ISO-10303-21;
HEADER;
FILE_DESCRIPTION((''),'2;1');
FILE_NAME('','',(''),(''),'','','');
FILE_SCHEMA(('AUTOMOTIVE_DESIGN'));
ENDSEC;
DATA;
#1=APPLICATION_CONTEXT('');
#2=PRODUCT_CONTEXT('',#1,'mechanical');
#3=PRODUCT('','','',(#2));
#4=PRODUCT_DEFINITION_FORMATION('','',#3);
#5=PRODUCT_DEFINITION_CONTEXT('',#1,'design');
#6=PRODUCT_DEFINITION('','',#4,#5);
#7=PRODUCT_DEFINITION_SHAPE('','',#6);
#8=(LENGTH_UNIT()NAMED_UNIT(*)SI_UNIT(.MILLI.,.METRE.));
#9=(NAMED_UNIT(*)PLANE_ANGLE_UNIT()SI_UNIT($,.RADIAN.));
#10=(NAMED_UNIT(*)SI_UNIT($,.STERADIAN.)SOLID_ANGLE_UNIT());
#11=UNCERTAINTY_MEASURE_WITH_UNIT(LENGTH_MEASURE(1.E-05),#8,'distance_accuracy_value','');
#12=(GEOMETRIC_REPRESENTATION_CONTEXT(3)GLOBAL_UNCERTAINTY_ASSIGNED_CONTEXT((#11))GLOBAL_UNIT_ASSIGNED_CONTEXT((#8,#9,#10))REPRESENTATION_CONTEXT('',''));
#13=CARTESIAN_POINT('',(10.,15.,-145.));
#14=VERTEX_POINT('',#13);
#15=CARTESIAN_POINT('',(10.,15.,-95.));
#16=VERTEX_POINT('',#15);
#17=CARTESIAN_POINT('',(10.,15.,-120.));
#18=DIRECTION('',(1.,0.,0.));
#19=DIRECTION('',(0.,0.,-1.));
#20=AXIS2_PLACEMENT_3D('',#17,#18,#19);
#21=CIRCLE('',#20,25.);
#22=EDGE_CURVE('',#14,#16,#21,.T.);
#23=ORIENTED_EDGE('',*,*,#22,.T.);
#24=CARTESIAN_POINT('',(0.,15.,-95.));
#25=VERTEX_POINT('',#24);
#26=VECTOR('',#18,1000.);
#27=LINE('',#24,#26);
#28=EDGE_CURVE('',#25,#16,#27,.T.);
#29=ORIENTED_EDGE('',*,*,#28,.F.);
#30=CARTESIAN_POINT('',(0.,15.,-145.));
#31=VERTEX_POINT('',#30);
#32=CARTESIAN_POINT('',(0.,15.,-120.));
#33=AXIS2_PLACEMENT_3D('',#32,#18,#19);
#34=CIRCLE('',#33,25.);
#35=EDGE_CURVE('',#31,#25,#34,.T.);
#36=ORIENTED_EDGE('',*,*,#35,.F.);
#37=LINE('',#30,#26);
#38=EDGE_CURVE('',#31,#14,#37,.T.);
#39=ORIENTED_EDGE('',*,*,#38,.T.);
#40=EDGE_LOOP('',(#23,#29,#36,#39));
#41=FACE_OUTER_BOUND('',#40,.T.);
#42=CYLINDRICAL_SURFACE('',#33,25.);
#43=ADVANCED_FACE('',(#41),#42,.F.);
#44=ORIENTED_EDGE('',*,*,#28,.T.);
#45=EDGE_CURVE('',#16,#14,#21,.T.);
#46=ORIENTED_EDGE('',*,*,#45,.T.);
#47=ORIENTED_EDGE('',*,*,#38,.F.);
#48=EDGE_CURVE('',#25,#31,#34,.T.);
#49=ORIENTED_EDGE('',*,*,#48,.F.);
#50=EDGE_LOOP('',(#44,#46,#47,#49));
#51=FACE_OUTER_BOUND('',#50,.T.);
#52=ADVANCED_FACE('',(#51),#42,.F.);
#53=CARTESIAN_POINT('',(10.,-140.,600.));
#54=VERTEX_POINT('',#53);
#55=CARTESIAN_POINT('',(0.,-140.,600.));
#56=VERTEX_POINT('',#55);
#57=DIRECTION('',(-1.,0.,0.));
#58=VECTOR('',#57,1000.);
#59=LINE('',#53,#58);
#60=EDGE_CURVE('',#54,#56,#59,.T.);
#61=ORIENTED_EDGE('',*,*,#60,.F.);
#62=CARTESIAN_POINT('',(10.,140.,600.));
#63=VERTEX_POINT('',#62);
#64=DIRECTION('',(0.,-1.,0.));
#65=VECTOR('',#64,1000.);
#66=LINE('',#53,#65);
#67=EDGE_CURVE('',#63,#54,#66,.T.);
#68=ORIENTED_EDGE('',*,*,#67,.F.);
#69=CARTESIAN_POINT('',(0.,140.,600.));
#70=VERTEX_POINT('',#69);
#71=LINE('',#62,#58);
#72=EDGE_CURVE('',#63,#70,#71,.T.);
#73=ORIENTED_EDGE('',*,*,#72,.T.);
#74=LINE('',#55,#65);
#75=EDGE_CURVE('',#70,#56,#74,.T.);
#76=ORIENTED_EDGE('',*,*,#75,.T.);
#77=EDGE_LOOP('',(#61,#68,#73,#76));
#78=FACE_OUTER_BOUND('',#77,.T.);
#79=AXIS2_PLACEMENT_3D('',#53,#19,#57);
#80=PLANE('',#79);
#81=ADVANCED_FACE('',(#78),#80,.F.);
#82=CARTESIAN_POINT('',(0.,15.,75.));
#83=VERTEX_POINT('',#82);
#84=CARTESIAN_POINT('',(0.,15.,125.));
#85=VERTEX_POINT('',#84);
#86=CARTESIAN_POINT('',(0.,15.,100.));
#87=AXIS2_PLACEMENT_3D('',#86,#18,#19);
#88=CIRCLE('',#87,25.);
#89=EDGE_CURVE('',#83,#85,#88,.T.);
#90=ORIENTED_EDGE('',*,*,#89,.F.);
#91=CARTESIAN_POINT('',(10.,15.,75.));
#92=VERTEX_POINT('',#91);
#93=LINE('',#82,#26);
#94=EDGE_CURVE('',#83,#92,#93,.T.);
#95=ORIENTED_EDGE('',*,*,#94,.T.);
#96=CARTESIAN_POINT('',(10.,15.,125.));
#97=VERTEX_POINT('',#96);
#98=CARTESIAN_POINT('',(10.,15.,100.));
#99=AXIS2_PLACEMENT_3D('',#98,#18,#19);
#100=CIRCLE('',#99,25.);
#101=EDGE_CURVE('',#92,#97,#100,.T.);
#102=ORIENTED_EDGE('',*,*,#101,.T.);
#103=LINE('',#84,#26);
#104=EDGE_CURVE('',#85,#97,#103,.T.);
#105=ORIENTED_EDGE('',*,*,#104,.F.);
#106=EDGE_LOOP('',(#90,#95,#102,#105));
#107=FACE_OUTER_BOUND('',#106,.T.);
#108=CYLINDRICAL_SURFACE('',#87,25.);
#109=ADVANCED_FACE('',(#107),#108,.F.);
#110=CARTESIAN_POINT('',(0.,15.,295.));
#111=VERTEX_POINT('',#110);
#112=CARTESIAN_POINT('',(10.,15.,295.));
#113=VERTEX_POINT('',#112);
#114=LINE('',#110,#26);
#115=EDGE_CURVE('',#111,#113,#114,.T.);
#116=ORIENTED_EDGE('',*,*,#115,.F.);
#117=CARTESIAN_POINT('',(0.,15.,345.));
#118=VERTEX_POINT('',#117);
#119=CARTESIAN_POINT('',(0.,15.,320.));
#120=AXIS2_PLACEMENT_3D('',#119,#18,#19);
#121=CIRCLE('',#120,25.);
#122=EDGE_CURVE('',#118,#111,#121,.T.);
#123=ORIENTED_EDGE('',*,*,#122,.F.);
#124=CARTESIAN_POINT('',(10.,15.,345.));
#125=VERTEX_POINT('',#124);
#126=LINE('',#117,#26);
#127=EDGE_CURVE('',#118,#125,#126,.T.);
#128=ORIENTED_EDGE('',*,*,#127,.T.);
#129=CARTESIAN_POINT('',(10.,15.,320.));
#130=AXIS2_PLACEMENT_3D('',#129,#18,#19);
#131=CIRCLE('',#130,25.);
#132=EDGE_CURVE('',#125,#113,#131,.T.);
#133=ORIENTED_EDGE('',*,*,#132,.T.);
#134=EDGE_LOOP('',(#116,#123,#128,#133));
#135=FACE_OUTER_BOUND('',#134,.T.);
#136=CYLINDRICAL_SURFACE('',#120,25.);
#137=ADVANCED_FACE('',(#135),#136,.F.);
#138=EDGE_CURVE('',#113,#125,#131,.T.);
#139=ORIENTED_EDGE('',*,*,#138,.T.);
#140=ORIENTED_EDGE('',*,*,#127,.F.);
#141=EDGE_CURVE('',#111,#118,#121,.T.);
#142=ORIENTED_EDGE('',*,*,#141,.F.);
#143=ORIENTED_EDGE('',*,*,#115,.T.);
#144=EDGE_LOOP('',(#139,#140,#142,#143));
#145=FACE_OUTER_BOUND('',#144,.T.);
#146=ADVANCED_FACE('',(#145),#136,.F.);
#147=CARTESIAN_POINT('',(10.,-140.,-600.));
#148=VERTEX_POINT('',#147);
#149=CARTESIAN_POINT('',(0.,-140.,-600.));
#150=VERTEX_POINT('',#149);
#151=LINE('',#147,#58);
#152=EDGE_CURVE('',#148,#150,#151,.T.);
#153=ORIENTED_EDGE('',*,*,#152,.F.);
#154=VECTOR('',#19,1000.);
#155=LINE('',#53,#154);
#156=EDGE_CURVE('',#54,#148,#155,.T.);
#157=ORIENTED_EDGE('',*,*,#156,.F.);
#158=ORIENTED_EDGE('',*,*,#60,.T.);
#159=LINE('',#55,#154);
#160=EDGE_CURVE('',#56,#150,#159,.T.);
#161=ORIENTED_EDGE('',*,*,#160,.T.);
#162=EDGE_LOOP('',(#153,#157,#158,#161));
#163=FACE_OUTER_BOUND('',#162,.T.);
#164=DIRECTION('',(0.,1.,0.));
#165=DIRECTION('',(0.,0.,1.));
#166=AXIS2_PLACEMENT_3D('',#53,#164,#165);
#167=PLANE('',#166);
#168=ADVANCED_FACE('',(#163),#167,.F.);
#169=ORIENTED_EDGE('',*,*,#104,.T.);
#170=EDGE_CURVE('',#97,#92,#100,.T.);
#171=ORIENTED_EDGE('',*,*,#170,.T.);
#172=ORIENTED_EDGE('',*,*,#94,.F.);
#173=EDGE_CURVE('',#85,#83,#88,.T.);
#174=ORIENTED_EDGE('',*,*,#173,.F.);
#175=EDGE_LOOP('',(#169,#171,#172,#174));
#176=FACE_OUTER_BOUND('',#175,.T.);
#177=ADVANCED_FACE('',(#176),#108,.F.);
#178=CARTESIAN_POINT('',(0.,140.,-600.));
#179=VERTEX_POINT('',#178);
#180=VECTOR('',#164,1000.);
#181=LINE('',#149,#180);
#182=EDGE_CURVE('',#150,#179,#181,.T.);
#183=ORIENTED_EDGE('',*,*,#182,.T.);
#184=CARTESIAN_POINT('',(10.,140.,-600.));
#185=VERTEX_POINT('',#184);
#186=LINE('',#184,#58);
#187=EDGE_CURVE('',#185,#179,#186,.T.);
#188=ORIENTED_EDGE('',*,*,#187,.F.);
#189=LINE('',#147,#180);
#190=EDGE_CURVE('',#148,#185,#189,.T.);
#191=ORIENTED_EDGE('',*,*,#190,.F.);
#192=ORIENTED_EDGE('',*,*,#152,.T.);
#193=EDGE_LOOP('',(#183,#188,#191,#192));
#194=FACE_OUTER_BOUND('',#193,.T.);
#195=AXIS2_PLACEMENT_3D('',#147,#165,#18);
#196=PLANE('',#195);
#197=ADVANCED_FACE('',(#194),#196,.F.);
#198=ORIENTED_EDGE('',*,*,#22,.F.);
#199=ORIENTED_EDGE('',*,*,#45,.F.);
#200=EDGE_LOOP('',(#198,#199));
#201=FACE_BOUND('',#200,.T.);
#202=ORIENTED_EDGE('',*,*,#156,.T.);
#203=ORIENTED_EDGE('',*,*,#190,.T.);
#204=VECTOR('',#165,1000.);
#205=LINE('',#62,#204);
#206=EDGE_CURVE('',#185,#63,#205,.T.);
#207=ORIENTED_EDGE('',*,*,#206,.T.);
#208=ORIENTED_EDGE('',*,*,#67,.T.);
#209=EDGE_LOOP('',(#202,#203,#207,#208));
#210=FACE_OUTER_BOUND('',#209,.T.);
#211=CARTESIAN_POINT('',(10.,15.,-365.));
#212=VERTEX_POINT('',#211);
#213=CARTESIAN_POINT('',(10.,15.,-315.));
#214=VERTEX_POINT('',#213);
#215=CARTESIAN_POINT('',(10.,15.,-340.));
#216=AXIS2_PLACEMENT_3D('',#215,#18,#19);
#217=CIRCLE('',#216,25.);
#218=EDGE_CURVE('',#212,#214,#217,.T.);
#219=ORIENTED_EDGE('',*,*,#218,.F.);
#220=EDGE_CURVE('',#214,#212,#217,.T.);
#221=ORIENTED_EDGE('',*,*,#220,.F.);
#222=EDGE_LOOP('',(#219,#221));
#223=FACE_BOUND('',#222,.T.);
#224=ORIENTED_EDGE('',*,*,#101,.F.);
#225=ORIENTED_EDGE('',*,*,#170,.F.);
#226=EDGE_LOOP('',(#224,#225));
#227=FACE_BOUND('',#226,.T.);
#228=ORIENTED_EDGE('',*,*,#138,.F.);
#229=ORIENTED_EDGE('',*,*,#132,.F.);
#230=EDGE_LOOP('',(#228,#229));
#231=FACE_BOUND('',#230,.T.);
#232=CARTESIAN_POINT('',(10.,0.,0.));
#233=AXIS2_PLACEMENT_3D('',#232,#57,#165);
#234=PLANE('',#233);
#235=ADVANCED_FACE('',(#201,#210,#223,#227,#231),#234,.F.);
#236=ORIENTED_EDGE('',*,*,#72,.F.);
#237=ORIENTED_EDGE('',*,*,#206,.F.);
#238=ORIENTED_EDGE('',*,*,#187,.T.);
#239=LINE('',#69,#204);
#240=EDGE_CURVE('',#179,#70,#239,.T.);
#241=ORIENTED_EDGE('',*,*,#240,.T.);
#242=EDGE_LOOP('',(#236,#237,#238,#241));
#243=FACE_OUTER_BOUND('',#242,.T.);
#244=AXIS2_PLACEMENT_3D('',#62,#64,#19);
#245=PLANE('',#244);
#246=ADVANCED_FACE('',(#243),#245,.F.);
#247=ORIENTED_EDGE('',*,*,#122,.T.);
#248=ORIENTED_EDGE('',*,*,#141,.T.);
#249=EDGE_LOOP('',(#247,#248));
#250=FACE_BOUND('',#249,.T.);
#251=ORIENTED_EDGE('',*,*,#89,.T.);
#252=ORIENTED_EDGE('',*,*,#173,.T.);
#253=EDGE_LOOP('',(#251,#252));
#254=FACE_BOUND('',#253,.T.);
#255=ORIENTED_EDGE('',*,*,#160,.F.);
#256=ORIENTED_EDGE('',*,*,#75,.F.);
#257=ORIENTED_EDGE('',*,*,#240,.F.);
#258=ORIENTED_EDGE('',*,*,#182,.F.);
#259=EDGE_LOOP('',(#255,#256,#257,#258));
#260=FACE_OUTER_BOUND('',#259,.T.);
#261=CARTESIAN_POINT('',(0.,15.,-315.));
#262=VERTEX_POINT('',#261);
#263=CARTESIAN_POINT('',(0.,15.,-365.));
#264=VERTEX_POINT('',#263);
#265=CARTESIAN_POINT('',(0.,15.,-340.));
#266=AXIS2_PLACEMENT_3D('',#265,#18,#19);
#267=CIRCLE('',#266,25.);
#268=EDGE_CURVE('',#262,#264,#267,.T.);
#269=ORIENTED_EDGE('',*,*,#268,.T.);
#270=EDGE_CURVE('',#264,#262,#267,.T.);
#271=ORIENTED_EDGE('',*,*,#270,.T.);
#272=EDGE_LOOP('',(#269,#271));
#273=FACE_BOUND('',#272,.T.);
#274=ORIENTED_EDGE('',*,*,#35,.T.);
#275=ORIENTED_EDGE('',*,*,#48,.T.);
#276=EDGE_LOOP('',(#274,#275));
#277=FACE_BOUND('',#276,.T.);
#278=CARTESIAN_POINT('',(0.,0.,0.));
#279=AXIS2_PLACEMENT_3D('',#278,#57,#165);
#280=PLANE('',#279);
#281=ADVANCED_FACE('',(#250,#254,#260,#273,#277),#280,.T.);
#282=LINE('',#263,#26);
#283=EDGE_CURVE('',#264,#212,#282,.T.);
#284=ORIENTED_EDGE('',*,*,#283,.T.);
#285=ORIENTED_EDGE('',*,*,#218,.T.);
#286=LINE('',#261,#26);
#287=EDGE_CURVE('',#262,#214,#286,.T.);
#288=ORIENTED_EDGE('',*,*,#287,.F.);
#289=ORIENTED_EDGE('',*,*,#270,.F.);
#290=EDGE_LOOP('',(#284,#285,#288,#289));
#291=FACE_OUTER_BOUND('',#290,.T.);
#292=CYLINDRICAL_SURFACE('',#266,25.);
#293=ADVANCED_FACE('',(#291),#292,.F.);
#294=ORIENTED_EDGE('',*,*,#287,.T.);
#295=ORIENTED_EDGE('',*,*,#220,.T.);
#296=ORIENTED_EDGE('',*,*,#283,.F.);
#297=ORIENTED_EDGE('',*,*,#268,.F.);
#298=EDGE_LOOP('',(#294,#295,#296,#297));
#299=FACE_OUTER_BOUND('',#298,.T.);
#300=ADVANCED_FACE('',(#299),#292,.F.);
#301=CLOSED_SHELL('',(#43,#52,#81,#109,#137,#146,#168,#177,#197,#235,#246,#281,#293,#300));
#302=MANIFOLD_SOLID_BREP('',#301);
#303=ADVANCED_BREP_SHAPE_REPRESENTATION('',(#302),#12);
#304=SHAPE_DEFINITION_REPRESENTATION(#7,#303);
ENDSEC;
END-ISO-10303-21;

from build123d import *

# Parameters (mm, degrees)
SKETCH1_W           = 1200
SKETCH1_H           = 280
BOSS_EXTRUDE1_DEPTH = 10
SKETCH2_R           = 25
CUT_EXTRUDE1_DEPTH  = 10
LPATTERN1_COUNT     = 4
LPATTERN1_PITCH     = 220


with BuildPart() as part:
    # Sketch1 → Boss-Extrude1 (new body)
    with BuildSketch(Plane(origin=(0, 0, 0), x_dir=(0, 0, -1), z_dir=(1, 0, 0))):
        Rectangle(SKETCH1_W, SKETCH1_H)
    extrude(amount=BOSS_EXTRUDE1_DEPTH)

    # Sketch2 → Cut-Extrude1 (cut)
    with BuildSketch(Plane(origin=(10, 0, 0), x_dir=(0, 0, -1), z_dir=(1, 0, 0))):
        with Locations((-320, 15)):
            Circle(SKETCH2_R)
    cut_extrude1 = extrude(amount=-CUT_EXTRUDE1_DEPTH, mode=Mode.SUBTRACT)

    # LPattern1: Cut-Extrude1 ×4
    with Locations(*[(0, 0, -i * LPATTERN1_PITCH) for i in range(1, LPATTERN1_COUNT)]):
        add(cut_extrude1, mode=Mode.SUBTRACT)


solid = part.part
